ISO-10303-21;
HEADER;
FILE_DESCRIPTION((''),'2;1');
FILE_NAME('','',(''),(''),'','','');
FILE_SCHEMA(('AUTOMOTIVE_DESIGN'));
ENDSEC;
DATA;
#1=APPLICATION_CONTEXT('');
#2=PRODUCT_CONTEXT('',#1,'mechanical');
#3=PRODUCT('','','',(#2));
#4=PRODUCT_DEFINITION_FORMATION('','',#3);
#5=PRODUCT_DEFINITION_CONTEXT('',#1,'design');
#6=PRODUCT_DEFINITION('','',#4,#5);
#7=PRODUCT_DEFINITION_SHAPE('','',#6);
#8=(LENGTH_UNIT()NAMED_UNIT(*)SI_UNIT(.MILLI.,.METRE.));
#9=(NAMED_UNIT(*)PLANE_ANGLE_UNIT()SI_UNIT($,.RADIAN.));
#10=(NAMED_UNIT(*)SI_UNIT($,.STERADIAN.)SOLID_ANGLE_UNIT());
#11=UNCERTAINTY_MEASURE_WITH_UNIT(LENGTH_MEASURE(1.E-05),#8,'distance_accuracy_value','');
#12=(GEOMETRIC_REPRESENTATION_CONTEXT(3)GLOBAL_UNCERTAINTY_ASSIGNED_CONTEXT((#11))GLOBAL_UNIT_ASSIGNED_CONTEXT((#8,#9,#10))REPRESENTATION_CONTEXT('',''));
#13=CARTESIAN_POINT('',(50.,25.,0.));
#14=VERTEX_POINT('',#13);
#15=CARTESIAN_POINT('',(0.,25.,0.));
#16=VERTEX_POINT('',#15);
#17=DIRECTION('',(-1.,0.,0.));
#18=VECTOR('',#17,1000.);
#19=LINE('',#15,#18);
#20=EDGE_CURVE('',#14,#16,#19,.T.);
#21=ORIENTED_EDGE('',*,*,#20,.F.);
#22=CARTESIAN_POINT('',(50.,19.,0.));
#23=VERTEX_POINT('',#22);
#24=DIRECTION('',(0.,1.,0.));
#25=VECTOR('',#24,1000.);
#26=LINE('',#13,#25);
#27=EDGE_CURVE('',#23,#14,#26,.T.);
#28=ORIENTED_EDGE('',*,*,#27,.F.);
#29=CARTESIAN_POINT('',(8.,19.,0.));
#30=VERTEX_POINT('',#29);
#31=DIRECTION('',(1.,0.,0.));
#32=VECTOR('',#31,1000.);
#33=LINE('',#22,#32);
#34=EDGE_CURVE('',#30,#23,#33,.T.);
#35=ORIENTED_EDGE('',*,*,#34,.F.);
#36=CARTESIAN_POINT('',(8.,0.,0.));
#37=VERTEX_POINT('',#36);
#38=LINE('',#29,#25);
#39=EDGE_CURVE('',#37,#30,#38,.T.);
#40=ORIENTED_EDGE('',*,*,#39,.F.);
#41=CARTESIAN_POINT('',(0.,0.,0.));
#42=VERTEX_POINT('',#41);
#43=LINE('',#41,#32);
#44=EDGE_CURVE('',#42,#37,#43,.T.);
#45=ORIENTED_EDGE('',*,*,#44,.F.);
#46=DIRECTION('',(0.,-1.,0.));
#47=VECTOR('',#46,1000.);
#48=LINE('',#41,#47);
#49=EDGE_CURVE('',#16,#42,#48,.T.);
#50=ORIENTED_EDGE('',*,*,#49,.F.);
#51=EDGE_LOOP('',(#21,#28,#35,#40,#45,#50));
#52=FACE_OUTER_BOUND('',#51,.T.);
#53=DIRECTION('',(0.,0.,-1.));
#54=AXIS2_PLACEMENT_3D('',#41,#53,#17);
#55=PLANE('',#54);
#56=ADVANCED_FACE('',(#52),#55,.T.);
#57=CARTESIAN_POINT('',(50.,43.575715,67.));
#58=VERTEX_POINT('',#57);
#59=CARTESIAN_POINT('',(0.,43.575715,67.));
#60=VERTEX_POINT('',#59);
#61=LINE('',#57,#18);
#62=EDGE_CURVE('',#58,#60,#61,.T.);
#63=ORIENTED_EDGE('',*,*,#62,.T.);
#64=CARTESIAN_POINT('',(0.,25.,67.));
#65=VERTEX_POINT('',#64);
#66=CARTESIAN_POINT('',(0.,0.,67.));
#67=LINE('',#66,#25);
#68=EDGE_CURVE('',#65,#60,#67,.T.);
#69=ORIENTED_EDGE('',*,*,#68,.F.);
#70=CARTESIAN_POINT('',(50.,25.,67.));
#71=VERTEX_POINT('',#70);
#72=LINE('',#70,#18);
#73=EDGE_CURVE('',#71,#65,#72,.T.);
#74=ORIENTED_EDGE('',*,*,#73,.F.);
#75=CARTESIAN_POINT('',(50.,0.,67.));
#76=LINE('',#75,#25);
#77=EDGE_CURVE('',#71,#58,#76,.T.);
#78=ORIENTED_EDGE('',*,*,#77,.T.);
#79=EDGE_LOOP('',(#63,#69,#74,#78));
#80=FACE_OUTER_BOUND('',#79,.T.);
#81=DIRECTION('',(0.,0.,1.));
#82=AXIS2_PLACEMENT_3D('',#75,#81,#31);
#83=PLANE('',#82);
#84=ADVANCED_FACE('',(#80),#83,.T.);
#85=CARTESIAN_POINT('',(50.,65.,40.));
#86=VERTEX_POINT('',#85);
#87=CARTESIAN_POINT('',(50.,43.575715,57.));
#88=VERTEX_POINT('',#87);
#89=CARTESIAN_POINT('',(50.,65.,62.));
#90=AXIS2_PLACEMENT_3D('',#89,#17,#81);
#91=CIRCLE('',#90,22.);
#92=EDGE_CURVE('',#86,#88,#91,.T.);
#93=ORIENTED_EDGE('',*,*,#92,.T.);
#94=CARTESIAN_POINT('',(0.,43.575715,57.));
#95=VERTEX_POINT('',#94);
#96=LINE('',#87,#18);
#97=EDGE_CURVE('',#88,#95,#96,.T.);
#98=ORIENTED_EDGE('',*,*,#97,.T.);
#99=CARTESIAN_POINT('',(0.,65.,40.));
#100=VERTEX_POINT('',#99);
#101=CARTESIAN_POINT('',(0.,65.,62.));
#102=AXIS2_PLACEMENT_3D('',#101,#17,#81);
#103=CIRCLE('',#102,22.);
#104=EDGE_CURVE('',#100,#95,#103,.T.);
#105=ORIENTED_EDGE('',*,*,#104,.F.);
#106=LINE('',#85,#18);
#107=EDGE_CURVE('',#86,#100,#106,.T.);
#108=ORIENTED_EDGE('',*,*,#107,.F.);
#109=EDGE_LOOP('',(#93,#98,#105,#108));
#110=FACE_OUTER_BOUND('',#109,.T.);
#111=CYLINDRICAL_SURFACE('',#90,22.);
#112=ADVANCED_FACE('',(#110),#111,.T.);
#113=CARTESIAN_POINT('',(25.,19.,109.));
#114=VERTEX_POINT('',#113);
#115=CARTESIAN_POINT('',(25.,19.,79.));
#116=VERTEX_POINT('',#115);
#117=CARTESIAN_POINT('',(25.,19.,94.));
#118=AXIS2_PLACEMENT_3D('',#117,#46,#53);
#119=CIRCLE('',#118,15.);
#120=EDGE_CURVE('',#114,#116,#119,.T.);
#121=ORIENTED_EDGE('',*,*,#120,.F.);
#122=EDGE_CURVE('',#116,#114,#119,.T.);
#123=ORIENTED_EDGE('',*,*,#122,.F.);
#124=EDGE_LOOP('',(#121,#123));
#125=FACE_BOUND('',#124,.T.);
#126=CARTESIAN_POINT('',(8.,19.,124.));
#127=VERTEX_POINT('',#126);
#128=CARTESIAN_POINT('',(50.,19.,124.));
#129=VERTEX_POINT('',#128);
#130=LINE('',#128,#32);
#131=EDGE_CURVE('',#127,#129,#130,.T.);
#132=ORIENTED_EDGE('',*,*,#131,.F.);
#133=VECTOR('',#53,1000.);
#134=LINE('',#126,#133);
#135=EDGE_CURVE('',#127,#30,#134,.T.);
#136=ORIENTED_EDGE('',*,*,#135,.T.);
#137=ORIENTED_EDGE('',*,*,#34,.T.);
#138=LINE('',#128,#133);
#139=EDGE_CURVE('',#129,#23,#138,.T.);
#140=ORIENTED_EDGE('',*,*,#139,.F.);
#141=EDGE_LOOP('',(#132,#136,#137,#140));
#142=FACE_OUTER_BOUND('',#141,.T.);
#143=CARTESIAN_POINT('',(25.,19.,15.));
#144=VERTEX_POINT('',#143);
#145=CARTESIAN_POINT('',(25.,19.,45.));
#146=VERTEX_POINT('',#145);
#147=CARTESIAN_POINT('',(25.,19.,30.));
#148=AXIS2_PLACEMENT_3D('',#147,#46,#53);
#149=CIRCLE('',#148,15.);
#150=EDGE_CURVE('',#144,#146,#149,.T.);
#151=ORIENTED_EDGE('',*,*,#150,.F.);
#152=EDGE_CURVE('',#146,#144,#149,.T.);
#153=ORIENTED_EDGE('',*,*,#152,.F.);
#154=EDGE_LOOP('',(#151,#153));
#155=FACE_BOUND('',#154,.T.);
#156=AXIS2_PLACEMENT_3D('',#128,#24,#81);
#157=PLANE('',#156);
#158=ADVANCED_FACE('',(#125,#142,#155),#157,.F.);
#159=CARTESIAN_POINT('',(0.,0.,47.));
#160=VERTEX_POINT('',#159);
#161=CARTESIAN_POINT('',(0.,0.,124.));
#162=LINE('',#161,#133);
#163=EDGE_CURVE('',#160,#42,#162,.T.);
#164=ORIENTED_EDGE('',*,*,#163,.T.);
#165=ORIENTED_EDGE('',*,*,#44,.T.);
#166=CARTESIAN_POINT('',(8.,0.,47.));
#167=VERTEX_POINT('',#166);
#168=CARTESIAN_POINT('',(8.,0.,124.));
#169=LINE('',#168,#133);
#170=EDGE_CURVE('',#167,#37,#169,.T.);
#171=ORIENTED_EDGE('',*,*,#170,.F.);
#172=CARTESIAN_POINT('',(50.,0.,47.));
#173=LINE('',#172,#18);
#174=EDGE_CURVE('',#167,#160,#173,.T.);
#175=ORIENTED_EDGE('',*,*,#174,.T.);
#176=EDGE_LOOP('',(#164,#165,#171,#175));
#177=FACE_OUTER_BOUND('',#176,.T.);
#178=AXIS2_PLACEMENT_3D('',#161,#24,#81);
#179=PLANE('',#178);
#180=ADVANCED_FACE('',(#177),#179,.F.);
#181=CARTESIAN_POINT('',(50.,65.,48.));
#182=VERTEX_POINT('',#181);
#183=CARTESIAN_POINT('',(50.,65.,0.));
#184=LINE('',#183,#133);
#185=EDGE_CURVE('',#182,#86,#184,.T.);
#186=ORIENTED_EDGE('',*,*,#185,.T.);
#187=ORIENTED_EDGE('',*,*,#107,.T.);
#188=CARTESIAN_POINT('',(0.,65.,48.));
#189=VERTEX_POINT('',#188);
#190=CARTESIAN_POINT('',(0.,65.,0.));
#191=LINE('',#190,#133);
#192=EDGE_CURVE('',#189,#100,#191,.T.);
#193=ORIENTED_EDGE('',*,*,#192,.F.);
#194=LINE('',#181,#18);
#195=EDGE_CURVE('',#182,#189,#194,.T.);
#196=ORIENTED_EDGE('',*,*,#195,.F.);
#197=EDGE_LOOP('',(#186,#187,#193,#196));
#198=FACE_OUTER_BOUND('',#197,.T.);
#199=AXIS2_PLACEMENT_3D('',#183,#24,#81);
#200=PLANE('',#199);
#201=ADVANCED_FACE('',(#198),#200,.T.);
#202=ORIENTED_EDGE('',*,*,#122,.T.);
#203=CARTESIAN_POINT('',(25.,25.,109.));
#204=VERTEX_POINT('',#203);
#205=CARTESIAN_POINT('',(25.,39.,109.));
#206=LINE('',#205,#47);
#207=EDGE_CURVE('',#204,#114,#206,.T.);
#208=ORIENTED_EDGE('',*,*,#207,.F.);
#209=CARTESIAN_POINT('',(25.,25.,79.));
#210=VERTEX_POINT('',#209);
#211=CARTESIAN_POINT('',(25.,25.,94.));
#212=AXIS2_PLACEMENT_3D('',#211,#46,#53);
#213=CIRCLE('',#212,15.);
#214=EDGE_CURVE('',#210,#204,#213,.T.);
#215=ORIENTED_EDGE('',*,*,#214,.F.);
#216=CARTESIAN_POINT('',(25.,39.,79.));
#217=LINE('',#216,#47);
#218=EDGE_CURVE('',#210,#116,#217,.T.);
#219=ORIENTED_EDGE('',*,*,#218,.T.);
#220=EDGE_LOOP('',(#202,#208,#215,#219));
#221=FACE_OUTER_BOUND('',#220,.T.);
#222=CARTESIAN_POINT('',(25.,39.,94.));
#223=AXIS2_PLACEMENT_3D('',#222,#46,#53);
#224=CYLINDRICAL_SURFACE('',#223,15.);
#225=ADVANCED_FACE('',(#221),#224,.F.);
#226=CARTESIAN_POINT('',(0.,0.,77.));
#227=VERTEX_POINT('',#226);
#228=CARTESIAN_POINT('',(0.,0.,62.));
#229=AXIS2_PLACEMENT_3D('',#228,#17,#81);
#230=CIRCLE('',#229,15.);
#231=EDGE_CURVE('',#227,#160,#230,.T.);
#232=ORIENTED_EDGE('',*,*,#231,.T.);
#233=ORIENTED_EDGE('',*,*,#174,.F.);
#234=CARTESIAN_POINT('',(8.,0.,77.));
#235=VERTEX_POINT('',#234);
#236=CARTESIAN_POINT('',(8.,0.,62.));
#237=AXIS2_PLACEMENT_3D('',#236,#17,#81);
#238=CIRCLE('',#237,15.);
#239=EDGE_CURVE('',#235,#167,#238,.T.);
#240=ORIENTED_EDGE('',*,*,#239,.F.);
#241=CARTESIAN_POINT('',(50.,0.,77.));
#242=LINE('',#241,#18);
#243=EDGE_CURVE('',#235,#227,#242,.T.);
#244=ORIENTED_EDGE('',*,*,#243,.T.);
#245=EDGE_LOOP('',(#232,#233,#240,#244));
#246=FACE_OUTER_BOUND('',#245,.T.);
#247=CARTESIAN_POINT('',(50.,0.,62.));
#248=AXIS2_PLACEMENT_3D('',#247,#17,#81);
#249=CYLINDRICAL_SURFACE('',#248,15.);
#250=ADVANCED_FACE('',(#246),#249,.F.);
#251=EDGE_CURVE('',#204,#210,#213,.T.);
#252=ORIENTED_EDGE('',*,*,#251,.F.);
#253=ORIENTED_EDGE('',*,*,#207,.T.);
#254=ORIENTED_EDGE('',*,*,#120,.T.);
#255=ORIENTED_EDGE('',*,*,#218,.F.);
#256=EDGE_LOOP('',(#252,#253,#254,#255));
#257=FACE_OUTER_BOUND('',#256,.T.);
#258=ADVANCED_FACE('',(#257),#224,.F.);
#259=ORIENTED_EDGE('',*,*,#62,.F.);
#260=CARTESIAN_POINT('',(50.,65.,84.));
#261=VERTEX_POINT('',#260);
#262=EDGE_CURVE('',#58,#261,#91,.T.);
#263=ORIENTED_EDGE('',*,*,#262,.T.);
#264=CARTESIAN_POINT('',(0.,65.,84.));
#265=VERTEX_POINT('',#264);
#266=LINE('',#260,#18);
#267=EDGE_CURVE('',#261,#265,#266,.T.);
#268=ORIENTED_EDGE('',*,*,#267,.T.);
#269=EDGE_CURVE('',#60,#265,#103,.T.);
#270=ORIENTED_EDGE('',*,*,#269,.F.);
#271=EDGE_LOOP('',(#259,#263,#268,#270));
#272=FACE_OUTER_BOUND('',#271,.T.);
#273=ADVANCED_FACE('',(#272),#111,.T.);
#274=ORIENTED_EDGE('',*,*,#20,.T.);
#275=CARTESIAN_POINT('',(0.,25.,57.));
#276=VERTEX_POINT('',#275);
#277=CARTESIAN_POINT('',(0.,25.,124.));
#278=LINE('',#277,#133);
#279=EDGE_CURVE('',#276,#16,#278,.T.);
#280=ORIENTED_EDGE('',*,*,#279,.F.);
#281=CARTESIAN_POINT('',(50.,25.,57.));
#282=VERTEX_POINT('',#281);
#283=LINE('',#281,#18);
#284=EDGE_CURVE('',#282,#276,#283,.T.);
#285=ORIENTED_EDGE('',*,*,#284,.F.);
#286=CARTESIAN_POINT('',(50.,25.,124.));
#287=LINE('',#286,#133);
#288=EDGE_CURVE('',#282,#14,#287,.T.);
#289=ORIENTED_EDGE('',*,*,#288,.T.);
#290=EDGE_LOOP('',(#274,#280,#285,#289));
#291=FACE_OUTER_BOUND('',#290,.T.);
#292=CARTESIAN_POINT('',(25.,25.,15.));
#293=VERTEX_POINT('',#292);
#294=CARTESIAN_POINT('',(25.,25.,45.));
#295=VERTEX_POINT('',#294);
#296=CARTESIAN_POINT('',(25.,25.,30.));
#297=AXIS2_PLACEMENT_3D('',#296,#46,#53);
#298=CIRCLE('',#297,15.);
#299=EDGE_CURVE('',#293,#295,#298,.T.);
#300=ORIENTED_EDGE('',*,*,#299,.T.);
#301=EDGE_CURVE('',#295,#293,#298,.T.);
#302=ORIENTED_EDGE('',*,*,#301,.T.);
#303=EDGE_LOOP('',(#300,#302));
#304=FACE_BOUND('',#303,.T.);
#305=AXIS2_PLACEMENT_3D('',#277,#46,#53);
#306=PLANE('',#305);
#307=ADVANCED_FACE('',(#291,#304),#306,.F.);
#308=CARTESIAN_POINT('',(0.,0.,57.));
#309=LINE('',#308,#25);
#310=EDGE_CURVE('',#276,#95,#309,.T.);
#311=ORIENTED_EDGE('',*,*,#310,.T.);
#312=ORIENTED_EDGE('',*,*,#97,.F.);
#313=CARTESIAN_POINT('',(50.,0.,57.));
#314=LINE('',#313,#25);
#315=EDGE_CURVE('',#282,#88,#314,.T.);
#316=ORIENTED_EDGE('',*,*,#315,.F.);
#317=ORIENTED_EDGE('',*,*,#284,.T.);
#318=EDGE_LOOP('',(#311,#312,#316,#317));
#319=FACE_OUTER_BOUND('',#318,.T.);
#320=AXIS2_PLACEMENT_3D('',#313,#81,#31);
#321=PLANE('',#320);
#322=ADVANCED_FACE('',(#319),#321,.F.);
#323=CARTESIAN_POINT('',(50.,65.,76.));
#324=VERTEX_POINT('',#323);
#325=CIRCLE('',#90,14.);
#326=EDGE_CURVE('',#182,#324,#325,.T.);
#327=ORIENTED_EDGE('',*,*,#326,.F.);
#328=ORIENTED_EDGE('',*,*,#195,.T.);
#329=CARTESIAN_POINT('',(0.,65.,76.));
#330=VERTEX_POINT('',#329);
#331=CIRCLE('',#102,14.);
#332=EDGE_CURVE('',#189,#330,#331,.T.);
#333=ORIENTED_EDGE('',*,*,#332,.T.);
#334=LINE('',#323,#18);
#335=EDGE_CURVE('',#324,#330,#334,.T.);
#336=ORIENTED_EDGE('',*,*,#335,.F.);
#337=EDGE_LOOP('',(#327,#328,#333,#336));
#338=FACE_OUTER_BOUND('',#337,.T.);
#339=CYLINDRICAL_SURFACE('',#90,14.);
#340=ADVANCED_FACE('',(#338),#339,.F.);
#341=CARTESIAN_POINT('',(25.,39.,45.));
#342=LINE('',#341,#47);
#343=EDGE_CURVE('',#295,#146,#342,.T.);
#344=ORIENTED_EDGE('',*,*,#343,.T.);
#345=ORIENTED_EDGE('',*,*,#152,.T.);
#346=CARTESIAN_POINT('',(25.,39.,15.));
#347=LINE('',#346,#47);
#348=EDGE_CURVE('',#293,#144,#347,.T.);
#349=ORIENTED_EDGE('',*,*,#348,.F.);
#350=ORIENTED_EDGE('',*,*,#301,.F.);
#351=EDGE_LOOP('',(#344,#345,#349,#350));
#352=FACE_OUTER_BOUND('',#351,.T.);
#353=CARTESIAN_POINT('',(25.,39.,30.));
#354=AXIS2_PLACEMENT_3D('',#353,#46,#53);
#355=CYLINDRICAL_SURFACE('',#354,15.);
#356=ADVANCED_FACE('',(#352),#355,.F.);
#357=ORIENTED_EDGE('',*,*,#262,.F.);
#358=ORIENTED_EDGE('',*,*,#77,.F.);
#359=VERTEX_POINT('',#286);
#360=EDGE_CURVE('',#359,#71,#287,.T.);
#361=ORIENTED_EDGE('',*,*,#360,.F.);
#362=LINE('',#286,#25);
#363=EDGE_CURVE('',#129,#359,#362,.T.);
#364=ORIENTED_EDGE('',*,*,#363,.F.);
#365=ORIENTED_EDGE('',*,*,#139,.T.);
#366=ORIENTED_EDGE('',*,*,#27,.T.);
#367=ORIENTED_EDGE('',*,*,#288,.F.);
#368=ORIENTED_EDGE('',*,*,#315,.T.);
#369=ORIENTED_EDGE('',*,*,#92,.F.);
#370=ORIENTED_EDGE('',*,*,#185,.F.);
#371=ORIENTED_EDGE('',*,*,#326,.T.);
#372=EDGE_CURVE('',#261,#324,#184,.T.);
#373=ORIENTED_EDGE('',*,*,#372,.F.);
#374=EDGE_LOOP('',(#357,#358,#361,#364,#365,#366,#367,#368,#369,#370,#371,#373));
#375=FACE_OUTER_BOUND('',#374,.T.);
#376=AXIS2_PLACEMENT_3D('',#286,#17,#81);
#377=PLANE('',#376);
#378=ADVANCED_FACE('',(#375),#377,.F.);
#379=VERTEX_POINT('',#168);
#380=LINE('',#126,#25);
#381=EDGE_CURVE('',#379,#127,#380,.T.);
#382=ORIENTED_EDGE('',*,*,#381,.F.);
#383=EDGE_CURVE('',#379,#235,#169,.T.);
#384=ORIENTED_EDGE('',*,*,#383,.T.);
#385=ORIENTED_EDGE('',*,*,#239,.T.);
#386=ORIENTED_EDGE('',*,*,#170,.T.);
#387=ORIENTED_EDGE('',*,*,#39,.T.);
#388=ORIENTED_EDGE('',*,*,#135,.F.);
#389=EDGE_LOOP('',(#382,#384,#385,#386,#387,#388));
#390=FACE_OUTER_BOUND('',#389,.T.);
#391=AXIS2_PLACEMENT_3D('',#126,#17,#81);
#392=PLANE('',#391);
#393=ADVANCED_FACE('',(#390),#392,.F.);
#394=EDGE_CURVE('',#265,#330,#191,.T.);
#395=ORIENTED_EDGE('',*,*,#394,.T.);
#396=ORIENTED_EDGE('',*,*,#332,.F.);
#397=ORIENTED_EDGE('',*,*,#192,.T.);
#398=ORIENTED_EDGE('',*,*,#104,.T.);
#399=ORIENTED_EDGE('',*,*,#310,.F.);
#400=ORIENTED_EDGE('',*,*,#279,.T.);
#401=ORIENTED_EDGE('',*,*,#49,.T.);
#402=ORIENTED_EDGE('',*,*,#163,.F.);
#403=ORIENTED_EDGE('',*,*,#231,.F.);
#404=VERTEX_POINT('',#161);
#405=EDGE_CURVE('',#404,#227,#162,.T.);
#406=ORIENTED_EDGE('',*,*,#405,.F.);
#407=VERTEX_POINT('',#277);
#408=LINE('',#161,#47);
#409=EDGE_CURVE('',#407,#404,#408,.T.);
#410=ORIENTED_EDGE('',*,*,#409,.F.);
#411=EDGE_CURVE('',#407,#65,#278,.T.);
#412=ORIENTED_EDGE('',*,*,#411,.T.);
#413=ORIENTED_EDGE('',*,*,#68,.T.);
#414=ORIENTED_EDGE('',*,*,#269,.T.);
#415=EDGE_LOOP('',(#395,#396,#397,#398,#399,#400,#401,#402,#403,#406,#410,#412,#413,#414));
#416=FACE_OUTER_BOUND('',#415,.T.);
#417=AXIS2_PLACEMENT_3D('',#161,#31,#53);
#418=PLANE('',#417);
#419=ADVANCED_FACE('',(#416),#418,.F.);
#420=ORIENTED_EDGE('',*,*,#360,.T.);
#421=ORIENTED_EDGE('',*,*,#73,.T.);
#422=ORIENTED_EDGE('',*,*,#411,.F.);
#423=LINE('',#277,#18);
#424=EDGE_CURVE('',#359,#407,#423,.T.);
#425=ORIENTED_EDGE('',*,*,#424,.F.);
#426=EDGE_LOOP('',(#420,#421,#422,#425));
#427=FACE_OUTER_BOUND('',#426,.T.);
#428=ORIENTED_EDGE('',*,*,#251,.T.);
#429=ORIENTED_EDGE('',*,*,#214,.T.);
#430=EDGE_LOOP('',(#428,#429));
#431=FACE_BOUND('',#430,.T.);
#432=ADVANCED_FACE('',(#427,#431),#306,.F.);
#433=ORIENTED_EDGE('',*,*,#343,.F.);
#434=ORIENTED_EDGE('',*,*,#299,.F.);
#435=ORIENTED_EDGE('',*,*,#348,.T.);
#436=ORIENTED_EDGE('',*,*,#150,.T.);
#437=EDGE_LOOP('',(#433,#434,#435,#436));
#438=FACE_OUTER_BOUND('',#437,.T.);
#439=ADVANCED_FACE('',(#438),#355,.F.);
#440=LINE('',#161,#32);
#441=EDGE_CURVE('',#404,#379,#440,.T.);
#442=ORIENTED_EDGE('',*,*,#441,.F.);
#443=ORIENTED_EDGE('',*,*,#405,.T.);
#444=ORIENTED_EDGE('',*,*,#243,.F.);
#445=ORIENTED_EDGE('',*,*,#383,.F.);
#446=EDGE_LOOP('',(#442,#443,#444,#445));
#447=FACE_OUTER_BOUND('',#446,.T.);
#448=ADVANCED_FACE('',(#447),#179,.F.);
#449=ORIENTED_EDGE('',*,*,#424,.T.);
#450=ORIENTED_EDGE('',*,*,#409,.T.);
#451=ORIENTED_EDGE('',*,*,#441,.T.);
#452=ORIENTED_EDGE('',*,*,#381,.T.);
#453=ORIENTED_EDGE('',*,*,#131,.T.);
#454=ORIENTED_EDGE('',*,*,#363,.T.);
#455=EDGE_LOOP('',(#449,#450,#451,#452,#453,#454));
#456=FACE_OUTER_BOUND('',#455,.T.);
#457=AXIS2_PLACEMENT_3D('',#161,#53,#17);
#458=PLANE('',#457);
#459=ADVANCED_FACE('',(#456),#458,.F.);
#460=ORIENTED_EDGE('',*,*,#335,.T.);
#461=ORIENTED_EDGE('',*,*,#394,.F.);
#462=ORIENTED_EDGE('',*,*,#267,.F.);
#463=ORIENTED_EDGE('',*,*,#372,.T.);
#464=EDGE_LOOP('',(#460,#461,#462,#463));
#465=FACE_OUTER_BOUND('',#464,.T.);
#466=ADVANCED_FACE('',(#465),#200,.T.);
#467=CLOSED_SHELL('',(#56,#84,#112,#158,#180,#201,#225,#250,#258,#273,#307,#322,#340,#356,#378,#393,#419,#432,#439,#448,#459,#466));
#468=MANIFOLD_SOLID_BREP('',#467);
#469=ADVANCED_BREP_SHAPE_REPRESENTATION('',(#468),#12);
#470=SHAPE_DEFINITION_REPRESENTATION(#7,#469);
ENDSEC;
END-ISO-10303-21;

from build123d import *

# Parameters (mm, degrees)
BASE_ANGLE_DEPTH           = 124
SADDLE_BOSS_DEPTH          = 50
SADDLE_SEAT_CUT_DEPTH      = 50
RELIEF_CUT_DEPTH           = 50
MOUNTING_HOLES_SKETCH_R    = 15
MOUNTING_HOLES_2X_30_DEPTH = 20


with BuildPart() as part:
    # Base Angle Profile Sketch → Base Angle (new body)
    with BuildSketch(Plane.XY):
        Polygon((0, 0), (0, 25), (50, 25), (50, 19), (8, 19), (8, 0), align=None)
    extrude(amount=BASE_ANGLE_DEPTH)

    # Saddle Boss Sketch → Saddle Boss (add)
    with BuildSketch(Plane.ZY):
        with BuildLine():
            Line((84, 65), (62, 65))
            Line((62, 65), (40, 65))
            ThreePointArc((40, 65), (44.76631206, 51.325205669), (57, 43.575714714))
            Line((57, 43.575714714), (57, 25))
            Line((57, 25), (67, 25))
            Line((67, 25), (67, 43.575714714))
            ThreePointArc((67, 43.575714714), (79.23368794, 51.325205669), (84, 65))
        make_face()
    extrude(amount=-SADDLE_BOSS_DEPTH)

    # Saddle Seat Sketch → Saddle Seat Cut (cut)
    with BuildSketch(Plane.ZY):
        with BuildLine():
            Line((48, 65), (76, 65))
            ThreePointArc((76, 65), (62, 51), (48, 65))
        make_face()
    extrude(amount=-SADDLE_SEAT_CUT_DEPTH, mode=Mode.SUBTRACT)

    # Relief Cut Sketch → Relief Cut (cut)
    with BuildSketch(Plane.ZY):
        with BuildLine():
            Line((47, 0), (77, 0))
            ThreePointArc((77, 0), (62, 15), (47, 0))
        make_face()
    extrude(amount=-RELIEF_CUT_DEPTH, mode=Mode.SUBTRACT)

    # Mounting Holes Sketch → Mounting Holes 2xØ30 (cut)
    with BuildSketch(Plane.XZ.offset(-19)):
        with Locations(Location((25, 94, 0), (0, 0, 270))):
            Circle(MOUNTING_HOLES_SKETCH_R)
        with Locations(Location((25, 30, 0), (0, 0, 270))):
            Circle(MOUNTING_HOLES_SKETCH_R)
    extrude(amount=-MOUNTING_HOLES_2X_30_DEPTH, mode=Mode.SUBTRACT)


solid = part.part
